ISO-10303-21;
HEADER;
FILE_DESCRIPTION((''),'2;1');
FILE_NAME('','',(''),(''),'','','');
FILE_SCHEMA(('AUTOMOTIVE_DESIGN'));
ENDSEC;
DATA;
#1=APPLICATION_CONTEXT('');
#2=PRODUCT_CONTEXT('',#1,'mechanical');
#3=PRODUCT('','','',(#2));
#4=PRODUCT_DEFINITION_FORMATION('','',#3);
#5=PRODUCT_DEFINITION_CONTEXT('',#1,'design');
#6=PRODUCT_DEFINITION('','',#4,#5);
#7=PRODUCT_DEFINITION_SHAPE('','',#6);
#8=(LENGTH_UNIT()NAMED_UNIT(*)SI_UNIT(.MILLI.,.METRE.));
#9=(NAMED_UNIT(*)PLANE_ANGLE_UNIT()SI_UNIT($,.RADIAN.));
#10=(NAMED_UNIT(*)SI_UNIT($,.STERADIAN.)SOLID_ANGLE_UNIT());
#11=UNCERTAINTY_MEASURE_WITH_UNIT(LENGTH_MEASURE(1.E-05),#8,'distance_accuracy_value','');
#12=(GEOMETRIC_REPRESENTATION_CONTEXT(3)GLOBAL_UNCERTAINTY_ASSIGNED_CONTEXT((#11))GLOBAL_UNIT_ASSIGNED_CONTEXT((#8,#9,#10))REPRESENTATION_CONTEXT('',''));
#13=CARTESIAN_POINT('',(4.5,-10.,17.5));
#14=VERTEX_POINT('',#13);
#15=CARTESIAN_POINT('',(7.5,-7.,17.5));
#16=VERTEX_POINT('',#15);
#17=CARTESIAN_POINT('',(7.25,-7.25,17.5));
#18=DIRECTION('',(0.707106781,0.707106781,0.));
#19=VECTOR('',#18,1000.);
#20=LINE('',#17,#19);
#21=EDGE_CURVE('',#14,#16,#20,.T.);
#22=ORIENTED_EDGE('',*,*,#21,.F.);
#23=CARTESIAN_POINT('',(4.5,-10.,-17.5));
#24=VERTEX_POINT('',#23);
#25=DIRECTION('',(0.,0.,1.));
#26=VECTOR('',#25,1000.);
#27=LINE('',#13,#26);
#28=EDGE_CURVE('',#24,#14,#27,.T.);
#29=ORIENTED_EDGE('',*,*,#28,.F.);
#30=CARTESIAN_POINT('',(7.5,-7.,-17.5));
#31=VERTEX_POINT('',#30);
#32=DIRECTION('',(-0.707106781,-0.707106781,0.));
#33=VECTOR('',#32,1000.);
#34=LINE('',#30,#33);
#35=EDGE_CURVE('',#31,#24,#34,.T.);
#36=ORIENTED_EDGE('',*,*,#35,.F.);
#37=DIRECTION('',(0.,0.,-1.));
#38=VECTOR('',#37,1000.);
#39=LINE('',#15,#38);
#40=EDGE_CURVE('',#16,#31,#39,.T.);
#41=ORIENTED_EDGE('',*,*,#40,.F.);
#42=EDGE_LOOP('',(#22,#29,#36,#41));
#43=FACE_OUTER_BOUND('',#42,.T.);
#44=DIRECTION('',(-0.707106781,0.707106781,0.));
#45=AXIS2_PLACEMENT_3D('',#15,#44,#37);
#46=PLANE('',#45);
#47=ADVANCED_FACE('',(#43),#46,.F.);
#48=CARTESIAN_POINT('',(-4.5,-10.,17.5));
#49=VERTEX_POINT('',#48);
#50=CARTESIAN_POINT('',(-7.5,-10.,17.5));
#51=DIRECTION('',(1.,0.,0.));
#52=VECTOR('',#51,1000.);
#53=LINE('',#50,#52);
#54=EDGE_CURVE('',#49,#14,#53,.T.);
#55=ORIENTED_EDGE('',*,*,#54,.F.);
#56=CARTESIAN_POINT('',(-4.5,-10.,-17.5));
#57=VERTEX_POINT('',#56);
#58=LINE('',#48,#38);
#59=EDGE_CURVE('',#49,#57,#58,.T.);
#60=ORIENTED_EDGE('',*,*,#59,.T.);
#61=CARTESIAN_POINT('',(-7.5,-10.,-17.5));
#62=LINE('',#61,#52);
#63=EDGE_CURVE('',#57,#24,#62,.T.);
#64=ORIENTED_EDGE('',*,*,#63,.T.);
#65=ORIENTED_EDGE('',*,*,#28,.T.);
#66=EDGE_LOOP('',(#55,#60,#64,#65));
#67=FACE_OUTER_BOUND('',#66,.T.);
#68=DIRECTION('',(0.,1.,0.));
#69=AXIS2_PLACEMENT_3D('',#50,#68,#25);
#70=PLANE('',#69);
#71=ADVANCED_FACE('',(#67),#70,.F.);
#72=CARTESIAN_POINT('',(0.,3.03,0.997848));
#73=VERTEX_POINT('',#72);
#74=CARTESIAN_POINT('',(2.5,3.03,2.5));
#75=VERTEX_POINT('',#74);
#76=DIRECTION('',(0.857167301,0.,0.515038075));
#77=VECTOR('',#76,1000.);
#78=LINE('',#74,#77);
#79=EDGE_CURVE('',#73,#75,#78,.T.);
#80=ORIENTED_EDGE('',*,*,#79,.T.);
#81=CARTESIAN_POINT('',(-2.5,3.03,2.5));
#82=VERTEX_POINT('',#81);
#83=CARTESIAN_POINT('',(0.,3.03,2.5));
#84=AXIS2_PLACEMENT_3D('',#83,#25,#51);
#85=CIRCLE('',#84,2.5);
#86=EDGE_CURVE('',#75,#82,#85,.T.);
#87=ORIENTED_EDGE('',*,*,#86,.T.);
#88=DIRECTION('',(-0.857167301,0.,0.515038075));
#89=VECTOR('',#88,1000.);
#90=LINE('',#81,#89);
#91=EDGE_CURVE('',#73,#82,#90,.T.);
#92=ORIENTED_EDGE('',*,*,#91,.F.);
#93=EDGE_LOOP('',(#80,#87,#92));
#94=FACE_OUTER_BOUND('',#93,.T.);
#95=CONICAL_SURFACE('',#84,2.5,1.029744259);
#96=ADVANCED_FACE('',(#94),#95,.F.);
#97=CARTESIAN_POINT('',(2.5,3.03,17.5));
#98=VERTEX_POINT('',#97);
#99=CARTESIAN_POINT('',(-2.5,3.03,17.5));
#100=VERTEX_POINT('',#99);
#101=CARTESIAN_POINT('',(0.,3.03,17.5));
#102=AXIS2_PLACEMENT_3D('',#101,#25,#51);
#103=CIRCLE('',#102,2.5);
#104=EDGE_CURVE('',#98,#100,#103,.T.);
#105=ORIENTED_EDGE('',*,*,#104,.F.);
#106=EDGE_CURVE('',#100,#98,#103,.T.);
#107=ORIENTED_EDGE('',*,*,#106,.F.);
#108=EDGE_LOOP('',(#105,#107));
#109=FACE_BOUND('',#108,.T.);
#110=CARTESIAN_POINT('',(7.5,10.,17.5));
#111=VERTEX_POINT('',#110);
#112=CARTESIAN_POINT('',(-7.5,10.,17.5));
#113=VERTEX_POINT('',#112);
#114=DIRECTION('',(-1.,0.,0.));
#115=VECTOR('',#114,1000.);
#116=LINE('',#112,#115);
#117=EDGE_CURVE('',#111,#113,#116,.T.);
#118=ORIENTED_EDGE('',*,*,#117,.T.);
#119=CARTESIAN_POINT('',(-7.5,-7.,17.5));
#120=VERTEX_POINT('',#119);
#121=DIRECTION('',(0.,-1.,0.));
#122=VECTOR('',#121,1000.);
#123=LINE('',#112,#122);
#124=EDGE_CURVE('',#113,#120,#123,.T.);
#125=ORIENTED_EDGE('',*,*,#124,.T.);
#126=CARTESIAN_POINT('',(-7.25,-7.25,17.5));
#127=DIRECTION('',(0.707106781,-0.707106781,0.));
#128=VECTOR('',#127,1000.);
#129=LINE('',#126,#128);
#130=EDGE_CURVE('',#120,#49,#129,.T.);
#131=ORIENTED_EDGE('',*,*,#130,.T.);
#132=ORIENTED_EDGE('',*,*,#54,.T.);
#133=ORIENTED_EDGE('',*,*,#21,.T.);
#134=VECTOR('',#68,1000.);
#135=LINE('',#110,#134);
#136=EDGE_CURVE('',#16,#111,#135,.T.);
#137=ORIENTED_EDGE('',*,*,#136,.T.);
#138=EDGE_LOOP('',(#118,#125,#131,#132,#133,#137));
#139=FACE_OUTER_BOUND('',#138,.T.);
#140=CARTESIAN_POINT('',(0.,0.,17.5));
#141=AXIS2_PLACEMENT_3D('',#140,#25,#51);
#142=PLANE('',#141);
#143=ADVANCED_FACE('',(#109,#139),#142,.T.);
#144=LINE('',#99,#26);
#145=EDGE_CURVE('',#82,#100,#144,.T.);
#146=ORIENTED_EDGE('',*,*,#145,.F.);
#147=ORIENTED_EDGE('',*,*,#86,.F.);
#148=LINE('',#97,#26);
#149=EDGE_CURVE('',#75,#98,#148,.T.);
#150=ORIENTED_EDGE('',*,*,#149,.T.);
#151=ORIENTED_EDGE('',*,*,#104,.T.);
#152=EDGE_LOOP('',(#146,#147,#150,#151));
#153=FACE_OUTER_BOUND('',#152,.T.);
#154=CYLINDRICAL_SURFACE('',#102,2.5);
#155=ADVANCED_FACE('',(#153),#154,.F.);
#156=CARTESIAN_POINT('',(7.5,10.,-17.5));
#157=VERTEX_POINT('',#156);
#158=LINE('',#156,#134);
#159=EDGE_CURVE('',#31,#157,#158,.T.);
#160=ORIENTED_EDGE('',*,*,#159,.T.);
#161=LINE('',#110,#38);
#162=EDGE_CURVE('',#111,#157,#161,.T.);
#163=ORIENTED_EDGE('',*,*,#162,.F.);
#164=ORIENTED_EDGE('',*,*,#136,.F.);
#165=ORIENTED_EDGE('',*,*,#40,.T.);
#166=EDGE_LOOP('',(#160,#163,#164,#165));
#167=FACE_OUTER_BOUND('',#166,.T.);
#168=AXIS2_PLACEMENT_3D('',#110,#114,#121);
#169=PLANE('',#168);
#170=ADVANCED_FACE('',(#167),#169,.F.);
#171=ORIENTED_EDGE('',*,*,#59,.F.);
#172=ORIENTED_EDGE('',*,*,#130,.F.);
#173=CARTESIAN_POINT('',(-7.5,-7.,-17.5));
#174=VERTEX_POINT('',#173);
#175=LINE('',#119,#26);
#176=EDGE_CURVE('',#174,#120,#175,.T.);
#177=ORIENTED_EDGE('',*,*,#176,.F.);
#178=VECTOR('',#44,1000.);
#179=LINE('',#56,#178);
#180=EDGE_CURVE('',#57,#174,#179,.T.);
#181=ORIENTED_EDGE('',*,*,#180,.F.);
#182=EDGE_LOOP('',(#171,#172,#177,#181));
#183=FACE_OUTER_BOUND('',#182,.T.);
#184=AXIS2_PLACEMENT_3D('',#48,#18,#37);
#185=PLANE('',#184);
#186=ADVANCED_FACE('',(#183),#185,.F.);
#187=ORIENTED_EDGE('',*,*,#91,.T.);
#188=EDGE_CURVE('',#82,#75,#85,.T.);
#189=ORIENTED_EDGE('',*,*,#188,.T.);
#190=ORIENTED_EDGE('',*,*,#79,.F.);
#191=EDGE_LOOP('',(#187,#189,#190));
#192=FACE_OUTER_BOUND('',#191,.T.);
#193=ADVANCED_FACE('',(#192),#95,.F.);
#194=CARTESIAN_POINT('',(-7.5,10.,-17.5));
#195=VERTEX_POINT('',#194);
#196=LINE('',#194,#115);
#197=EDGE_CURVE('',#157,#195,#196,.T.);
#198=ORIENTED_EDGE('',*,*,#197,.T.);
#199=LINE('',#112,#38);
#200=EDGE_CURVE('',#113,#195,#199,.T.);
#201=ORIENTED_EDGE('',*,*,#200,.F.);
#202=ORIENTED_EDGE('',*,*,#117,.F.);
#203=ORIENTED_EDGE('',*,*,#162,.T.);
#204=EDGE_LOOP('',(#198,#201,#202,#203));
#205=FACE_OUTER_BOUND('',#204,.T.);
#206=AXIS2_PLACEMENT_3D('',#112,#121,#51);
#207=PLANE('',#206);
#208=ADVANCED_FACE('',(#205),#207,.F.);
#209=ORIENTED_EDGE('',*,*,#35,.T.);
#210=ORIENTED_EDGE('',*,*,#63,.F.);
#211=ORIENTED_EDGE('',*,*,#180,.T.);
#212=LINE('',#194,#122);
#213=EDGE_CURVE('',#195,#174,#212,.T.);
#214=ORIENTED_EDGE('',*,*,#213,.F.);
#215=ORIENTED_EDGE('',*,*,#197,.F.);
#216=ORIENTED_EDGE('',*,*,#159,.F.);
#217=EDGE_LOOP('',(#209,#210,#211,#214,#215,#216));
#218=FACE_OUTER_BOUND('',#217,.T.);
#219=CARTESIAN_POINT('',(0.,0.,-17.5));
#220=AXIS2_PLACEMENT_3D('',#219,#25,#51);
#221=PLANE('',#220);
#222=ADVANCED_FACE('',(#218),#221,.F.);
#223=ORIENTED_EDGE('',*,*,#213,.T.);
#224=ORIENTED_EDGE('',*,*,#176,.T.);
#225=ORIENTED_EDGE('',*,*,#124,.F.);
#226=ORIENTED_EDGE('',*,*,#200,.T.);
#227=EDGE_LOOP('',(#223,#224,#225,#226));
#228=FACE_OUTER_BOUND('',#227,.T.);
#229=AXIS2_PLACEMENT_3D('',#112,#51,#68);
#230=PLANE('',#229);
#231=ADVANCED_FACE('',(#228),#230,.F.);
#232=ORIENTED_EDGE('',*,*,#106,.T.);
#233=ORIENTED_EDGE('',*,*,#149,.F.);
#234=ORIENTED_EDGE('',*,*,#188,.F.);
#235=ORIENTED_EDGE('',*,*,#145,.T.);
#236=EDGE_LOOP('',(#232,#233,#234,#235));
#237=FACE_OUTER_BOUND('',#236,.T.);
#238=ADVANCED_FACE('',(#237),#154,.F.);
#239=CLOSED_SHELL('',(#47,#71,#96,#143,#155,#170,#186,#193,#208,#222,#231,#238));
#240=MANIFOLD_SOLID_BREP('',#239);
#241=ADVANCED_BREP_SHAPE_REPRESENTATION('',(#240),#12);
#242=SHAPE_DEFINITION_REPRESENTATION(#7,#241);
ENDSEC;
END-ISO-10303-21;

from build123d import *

# Parameters (mm, degrees)
SKETCH1_W             = 15
SKETCH1_H             = 20
BOSS_EXTRUDE1_DEPTH   = 17.5
CHAMFER1_SIZE         = 3
M6_TAPPED_HOLE1_D     = 5
M6_TAPPED_HOLE1_DEPTH = 15
M6_TAPPED_HOLE1_TIP   = 1.502151548


with BuildPart() as part:
    # Sketch1 → Boss-Extrude1 (new, symmetric)
    with BuildSketch(Plane.XY):
        Rectangle(SKETCH1_W, SKETCH1_H)
    extrude(amount=BOSS_EXTRUDE1_DEPTH, both=True)

    # Chamfer1
    chamfer1_edges = [part.edges().sort_by_distance(p)[0] for p in [
        (7.5, -10, 0),
        (-7.5, -10, 0),
    ]]
    chamfer(chamfer1_edges, length=CHAMFER1_SIZE)

    # M6 Tapped Hole1
    with Locations(Plane.XY.offset(17.5)):
        with Locations((0, 3.03)):
            Hole(M6_TAPPED_HOLE1_D / 2, depth=M6_TAPPED_HOLE1_DEPTH)
            with Locations((0, 0, -(M6_TAPPED_HOLE1_DEPTH + M6_TAPPED_HOLE1_TIP / 2))):  # 118° drill point
                Cone(0, M6_TAPPED_HOLE1_D / 2, M6_TAPPED_HOLE1_TIP, mode=Mode.SUBTRACT)


solid = part.part
